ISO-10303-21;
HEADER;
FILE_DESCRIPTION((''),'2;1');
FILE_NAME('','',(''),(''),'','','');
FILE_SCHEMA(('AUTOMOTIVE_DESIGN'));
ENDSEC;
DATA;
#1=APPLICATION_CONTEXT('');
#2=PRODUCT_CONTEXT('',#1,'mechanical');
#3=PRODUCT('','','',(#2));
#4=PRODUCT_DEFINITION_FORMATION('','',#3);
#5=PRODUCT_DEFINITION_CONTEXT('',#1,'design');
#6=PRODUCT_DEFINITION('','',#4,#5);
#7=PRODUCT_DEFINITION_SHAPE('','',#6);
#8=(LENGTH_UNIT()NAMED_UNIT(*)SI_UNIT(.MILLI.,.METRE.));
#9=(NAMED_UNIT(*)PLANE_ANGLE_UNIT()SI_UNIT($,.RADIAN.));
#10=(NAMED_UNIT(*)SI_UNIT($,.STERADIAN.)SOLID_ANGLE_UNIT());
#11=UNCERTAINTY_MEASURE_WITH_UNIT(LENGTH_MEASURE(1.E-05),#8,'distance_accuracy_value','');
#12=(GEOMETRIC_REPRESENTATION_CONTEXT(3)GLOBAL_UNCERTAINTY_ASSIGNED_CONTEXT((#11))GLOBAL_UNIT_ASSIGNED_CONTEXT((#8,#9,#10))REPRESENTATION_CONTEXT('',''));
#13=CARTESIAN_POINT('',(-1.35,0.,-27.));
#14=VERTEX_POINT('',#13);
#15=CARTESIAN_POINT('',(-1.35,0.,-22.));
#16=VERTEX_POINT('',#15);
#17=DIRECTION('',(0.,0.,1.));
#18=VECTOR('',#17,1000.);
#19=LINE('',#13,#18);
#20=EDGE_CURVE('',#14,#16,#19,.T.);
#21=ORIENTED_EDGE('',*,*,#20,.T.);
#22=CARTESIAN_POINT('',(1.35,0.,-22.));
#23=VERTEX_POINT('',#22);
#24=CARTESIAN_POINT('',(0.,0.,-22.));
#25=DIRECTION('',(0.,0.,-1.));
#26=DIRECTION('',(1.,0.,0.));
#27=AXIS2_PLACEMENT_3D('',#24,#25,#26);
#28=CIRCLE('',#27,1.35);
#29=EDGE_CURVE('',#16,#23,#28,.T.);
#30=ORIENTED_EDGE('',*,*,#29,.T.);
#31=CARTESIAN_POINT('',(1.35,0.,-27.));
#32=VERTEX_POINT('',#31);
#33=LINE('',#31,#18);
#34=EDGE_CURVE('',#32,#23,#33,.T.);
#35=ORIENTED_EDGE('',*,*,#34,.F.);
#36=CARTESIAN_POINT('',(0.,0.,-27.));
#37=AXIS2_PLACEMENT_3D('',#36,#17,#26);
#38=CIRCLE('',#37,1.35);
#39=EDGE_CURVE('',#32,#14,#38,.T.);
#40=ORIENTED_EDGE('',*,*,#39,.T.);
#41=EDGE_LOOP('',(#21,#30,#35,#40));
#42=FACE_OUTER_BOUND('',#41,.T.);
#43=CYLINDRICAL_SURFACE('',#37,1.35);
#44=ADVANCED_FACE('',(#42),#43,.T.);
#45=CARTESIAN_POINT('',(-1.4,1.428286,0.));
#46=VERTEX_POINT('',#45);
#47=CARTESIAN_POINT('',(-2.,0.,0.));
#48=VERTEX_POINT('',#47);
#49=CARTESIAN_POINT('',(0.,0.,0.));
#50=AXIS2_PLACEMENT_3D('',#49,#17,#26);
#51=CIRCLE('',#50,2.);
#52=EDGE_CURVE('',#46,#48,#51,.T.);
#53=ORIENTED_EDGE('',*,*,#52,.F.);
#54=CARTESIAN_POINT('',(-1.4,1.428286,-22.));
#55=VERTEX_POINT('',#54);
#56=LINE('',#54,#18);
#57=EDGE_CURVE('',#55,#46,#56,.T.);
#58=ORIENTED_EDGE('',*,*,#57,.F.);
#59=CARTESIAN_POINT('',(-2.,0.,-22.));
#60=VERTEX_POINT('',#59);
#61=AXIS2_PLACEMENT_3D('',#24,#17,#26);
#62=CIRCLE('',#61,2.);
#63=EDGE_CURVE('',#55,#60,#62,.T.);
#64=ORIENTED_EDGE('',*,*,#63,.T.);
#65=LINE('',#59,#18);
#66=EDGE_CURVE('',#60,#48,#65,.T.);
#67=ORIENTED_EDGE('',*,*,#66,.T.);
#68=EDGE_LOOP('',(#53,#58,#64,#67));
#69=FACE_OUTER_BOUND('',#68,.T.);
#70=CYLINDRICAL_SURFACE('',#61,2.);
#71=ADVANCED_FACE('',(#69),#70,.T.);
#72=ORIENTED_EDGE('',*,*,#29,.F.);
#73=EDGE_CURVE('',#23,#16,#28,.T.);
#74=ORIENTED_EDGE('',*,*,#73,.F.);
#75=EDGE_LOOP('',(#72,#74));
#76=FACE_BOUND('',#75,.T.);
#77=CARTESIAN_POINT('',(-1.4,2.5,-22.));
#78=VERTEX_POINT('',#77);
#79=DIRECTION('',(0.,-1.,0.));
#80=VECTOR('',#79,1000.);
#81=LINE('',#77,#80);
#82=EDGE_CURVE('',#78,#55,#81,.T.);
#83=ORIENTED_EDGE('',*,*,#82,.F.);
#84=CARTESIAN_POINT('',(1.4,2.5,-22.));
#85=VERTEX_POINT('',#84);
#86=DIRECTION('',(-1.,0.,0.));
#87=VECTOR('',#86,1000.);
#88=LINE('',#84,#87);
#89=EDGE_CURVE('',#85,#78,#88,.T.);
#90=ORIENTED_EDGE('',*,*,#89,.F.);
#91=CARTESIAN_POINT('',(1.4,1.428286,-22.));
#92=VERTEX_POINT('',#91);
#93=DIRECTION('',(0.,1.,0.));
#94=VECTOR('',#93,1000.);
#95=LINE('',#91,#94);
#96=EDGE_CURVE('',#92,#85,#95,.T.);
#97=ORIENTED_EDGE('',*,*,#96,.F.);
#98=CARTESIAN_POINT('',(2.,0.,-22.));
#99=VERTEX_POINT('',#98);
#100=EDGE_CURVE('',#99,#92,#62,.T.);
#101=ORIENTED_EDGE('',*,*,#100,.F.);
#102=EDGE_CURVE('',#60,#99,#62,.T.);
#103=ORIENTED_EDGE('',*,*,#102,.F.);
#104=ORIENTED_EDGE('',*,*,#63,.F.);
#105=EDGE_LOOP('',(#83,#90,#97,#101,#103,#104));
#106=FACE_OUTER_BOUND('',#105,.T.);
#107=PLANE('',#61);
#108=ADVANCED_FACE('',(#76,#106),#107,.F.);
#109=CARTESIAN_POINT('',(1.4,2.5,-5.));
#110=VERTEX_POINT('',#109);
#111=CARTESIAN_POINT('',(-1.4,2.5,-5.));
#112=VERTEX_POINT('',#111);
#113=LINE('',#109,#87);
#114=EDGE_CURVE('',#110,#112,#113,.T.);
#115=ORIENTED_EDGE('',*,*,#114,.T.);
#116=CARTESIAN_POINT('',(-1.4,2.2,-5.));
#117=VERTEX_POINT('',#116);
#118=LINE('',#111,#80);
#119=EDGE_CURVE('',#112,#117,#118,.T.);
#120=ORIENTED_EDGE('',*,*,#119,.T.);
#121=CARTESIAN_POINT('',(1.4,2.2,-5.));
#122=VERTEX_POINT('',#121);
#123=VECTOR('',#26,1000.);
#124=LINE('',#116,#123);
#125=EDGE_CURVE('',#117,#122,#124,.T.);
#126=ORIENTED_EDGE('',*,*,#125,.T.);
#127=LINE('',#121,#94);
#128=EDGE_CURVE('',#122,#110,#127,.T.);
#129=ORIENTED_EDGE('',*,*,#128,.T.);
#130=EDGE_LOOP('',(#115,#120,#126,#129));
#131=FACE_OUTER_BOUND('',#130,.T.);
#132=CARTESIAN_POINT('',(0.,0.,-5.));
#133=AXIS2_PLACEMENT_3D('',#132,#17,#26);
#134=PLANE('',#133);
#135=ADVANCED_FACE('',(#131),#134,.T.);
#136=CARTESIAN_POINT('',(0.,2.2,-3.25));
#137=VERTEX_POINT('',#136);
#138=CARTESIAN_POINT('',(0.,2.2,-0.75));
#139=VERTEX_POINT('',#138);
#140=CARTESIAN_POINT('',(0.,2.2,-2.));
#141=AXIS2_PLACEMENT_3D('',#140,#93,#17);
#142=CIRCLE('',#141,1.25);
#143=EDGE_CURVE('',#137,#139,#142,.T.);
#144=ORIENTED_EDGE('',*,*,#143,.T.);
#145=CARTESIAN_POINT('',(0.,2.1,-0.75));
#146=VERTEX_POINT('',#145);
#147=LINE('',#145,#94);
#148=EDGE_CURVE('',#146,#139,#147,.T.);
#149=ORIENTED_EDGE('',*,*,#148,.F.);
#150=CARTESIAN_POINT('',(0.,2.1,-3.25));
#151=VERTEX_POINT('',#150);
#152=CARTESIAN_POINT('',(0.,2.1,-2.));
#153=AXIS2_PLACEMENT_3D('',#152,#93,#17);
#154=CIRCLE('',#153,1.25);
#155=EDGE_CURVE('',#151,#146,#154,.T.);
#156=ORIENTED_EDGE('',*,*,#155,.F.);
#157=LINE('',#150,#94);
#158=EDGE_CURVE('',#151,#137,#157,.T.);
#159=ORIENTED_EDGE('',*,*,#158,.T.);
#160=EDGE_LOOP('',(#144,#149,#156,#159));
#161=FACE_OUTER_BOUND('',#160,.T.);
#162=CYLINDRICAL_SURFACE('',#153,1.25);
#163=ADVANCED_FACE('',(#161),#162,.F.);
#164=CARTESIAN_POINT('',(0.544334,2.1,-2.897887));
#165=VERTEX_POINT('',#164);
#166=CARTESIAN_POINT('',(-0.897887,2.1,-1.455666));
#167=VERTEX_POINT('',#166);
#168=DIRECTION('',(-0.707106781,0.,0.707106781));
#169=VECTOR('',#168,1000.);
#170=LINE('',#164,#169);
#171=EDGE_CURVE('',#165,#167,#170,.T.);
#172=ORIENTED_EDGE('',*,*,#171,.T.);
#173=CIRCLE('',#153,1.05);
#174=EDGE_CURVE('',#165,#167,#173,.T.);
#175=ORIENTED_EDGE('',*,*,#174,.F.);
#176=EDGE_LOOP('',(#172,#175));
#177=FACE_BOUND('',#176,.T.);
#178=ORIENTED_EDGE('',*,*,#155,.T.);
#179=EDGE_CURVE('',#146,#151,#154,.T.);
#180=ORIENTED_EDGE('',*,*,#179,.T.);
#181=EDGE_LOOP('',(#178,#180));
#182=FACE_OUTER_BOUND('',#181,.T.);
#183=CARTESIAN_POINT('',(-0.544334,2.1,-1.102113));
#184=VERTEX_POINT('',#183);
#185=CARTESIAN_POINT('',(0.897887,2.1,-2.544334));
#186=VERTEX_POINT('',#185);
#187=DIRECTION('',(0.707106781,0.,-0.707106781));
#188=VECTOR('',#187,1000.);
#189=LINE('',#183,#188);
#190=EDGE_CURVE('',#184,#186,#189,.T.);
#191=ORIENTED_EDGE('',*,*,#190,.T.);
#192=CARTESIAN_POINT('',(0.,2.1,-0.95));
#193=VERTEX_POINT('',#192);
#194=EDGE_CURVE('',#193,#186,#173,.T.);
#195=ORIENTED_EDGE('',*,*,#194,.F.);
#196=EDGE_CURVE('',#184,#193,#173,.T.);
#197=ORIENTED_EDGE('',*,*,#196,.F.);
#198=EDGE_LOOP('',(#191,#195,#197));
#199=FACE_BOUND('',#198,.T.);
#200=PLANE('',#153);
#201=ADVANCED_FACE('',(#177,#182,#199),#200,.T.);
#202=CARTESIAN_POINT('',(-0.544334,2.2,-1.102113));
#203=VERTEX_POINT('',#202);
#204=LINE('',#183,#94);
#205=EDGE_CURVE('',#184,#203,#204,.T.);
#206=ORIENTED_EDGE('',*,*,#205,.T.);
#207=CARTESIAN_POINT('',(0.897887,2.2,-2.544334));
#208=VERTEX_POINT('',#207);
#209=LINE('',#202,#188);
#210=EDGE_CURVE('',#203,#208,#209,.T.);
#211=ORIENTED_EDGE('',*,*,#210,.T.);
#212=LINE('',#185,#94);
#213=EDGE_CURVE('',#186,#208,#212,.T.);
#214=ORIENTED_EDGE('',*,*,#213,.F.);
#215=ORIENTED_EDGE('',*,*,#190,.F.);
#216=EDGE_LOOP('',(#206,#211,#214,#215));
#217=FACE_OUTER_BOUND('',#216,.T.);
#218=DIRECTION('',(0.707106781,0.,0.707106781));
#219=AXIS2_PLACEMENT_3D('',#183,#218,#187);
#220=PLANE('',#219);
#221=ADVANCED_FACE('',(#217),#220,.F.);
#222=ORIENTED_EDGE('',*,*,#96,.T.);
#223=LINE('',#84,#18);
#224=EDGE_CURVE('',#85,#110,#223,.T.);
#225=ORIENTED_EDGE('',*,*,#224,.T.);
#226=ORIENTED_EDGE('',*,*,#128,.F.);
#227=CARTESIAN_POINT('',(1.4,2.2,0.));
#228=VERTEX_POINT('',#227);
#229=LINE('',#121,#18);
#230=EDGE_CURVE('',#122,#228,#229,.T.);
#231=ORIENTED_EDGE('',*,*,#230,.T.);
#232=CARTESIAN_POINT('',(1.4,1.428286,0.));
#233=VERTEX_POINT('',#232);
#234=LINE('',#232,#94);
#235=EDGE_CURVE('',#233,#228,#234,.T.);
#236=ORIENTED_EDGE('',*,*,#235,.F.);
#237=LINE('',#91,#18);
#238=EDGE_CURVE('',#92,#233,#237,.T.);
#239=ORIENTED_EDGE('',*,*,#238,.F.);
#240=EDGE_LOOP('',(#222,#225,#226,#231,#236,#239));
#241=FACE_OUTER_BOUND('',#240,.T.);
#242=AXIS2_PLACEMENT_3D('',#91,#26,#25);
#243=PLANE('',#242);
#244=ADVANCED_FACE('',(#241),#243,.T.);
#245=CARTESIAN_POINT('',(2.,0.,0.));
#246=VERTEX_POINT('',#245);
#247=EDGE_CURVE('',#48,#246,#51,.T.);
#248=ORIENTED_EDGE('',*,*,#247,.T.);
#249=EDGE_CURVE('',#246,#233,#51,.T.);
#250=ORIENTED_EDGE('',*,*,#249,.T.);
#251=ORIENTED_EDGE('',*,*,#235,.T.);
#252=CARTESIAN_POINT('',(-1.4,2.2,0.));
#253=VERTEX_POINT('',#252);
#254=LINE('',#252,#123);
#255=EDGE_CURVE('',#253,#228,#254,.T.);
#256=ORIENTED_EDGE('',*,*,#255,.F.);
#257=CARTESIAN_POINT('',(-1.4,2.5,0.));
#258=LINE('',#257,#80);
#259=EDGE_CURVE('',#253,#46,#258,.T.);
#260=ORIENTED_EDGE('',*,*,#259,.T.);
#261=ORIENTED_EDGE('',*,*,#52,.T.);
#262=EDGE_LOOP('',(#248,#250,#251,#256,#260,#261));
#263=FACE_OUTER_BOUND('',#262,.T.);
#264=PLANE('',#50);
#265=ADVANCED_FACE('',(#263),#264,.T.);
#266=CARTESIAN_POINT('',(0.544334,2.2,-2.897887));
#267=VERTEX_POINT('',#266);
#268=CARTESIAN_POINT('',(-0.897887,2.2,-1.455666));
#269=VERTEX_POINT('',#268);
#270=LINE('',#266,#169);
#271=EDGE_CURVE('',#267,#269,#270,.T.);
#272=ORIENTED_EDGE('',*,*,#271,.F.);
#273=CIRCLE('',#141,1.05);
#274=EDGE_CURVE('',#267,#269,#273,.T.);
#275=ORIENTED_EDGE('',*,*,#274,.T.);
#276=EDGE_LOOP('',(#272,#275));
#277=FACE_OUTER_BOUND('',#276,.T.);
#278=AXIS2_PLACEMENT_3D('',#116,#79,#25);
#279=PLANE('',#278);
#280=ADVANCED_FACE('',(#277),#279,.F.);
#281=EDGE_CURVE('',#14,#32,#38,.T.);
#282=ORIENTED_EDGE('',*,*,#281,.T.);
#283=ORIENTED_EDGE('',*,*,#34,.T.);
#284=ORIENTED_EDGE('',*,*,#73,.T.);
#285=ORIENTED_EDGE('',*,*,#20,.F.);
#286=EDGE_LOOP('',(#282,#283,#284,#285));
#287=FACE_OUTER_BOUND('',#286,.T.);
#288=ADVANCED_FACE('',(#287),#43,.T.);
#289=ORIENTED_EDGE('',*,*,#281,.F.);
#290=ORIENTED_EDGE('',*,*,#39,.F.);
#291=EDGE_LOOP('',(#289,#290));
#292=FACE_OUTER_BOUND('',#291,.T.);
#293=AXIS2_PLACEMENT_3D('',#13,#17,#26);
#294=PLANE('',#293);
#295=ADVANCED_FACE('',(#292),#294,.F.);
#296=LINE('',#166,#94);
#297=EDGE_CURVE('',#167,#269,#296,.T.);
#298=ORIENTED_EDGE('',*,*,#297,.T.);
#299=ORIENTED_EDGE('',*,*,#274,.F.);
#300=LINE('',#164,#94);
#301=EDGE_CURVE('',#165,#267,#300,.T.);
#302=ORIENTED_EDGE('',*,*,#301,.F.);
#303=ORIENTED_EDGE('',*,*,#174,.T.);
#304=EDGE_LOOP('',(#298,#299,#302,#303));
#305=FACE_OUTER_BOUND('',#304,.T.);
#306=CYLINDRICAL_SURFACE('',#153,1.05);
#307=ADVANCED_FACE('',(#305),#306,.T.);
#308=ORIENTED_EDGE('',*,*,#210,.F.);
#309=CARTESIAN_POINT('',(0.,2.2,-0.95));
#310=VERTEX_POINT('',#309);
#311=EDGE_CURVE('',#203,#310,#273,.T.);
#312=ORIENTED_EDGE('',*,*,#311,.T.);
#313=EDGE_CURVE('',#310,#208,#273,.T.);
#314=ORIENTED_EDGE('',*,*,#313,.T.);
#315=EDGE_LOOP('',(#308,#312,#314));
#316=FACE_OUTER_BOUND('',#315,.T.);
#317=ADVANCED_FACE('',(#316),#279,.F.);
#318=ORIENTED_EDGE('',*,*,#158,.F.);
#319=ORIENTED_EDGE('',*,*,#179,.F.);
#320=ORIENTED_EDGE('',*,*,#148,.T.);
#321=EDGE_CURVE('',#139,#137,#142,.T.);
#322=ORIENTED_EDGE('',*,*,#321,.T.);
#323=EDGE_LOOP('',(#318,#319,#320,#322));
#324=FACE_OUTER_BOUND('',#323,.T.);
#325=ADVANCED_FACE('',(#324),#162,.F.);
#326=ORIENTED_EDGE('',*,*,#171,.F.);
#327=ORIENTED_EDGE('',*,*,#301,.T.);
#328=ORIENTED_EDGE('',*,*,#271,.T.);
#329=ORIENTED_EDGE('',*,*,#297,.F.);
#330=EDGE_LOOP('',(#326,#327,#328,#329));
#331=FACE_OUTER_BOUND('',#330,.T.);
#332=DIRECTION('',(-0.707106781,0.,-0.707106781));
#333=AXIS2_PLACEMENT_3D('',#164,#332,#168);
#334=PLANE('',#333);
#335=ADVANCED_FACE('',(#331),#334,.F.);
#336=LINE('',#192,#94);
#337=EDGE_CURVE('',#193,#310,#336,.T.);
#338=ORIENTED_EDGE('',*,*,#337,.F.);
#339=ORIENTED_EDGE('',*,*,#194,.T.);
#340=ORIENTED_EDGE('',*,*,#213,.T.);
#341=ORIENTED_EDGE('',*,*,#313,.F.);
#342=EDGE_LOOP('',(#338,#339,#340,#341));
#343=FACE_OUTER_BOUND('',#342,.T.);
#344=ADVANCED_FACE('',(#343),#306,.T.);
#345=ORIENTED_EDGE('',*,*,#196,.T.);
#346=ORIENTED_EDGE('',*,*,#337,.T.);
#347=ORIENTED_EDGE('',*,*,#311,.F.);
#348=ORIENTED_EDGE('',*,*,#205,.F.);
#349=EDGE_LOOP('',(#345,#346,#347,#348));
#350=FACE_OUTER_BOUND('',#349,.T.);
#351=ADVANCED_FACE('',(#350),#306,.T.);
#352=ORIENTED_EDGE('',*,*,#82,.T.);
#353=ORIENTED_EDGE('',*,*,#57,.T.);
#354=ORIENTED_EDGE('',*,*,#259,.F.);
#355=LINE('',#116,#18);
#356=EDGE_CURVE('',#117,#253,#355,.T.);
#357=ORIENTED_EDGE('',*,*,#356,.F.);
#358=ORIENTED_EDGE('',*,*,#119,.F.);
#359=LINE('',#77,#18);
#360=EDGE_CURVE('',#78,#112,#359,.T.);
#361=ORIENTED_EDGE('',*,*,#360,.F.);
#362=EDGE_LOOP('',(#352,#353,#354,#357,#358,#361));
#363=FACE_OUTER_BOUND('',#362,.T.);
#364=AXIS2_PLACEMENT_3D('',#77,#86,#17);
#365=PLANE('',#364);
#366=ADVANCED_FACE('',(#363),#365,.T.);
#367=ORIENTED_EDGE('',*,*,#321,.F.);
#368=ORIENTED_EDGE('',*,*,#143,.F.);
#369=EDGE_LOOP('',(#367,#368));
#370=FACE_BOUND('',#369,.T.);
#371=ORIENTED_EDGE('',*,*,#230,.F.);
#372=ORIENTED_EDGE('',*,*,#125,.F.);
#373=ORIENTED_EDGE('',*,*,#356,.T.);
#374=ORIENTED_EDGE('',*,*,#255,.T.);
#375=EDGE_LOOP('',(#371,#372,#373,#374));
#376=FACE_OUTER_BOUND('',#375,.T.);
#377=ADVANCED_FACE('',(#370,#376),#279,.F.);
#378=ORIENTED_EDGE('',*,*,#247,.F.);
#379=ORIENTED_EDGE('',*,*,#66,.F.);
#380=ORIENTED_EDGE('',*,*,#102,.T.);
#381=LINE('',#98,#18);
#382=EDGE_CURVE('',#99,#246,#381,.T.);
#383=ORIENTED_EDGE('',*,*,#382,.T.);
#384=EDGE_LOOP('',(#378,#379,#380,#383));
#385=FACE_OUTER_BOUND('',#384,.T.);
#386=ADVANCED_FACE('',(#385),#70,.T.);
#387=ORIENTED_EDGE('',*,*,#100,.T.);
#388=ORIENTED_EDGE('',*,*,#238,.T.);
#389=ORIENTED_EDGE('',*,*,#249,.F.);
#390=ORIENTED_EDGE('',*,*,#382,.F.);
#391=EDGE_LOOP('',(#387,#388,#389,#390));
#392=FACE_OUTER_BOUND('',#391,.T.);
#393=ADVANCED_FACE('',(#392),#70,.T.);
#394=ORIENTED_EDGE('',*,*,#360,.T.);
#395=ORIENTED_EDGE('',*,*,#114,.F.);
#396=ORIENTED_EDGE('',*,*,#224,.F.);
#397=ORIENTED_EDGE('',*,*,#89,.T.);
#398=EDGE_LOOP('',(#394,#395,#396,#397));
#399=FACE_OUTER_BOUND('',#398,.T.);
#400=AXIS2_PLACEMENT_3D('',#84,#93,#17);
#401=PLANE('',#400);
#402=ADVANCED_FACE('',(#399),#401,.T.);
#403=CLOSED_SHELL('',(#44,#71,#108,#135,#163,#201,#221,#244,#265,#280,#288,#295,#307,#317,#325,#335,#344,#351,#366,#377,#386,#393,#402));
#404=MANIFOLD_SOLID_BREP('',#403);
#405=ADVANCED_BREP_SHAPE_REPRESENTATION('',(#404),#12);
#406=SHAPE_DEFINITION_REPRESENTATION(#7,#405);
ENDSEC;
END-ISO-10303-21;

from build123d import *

# Parameters (mm, degrees)
BOSS_EXTRUDE1_DEPTH = 22
SKETCH2_W           = 2.8
SKETCH2_H           = 0.3
CUT_EXTRUDE1_DEPTH  = 5
SKETCH3_R           = 1.25
SKETCH3_R_2         = 1.05
CUT_EXTRUDE2_DEPTH  = 0.1
CUT_EXTRUDE3_DEPTH  = 0.1
SKETCH5_W           = 1.35
SKETCH5_H           = 5


with BuildPart() as part:
    # Sketch1 → Boss-Extrude1 (new body)
    with BuildSketch(Plane.XY):
        with BuildLine():
            Line((1.4, 1.428285686), (1.4, 2.5))
            Line((1.4, 2.5), (-1.4, 2.5))
            Line((-1.4, 2.5), (-1.4, 1.428285686))
            ThreePointArc((-1.4, 1.428285686), (0, -2), (1.4, 1.428285686))
        make_face()
    extrude(amount=-BOSS_EXTRUDE1_DEPTH)

    # Sketch2 → Cut-Extrude1 (cut)
    with BuildSketch(Plane.XY):
        with Locations((0, 2.35)):
            Rectangle(SKETCH2_W, SKETCH2_H)
    extrude(amount=-CUT_EXTRUDE1_DEPTH, mode=Mode.SUBTRACT)

    # Sketch3 → Cut-Extrude2 (cut)
    with BuildSketch(Plane(origin=(0, 2.2, 0), x_dir=(1, 0, 0), z_dir=(0, 1, 0))):
        with Locations(Location((0, 2, 0), (0, 0, 270))):
            Circle(SKETCH3_R)
        with Locations(Location((0, 2, 0), (0, 0, 270))):
            Circle(SKETCH3_R_2, mode=Mode.SUBTRACT)
    extrude(amount=-CUT_EXTRUDE2_DEPTH, mode=Mode.SUBTRACT)

    # Sketch4 → Cut-Extrude3 (cut)
    with BuildSketch(Plane(origin=(0, 2.2, 0), x_dir=(1, 0, 0), z_dir=(0, 1, 0))):
        with BuildLine():
            Line((-0.54433356, 1.10211305), (0.89788695, 2.54433356))
            ThreePointArc((0.89788695, 2.54433356), (0.74246212, 2.74246212), (0.54433356, 2.89788695))
            Line((0.54433356, 2.89788695), (-0.89788695, 1.45566644))
            ThreePointArc((-0.89788695, 1.45566644), (-0.74246212, 1.25753788), (-0.54433356, 1.10211305))
        make_face()
    extrude(amount=-CUT_EXTRUDE3_DEPTH, mode=Mode.SUBTRACT)

    # Sketch5 → Revolve1 (revolve)
    with BuildSketch(Plane(origin=(0, 0, 0), x_dir=(1, 0, 0), z_dir=(0, 1, 0)), mode=Mode.PRIVATE) as revolve1_sk:
        with Locations((-0.675, 24.5)):
            Rectangle(SKETCH5_W, SKETCH5_H)
    revolve(revolve1_sk.sketch.rotate(Axis((0, 0, -27), (0, 0, 1)), 180), axis=Axis((0, 0, -27), (0, 0, 1)))


solid = part.part
